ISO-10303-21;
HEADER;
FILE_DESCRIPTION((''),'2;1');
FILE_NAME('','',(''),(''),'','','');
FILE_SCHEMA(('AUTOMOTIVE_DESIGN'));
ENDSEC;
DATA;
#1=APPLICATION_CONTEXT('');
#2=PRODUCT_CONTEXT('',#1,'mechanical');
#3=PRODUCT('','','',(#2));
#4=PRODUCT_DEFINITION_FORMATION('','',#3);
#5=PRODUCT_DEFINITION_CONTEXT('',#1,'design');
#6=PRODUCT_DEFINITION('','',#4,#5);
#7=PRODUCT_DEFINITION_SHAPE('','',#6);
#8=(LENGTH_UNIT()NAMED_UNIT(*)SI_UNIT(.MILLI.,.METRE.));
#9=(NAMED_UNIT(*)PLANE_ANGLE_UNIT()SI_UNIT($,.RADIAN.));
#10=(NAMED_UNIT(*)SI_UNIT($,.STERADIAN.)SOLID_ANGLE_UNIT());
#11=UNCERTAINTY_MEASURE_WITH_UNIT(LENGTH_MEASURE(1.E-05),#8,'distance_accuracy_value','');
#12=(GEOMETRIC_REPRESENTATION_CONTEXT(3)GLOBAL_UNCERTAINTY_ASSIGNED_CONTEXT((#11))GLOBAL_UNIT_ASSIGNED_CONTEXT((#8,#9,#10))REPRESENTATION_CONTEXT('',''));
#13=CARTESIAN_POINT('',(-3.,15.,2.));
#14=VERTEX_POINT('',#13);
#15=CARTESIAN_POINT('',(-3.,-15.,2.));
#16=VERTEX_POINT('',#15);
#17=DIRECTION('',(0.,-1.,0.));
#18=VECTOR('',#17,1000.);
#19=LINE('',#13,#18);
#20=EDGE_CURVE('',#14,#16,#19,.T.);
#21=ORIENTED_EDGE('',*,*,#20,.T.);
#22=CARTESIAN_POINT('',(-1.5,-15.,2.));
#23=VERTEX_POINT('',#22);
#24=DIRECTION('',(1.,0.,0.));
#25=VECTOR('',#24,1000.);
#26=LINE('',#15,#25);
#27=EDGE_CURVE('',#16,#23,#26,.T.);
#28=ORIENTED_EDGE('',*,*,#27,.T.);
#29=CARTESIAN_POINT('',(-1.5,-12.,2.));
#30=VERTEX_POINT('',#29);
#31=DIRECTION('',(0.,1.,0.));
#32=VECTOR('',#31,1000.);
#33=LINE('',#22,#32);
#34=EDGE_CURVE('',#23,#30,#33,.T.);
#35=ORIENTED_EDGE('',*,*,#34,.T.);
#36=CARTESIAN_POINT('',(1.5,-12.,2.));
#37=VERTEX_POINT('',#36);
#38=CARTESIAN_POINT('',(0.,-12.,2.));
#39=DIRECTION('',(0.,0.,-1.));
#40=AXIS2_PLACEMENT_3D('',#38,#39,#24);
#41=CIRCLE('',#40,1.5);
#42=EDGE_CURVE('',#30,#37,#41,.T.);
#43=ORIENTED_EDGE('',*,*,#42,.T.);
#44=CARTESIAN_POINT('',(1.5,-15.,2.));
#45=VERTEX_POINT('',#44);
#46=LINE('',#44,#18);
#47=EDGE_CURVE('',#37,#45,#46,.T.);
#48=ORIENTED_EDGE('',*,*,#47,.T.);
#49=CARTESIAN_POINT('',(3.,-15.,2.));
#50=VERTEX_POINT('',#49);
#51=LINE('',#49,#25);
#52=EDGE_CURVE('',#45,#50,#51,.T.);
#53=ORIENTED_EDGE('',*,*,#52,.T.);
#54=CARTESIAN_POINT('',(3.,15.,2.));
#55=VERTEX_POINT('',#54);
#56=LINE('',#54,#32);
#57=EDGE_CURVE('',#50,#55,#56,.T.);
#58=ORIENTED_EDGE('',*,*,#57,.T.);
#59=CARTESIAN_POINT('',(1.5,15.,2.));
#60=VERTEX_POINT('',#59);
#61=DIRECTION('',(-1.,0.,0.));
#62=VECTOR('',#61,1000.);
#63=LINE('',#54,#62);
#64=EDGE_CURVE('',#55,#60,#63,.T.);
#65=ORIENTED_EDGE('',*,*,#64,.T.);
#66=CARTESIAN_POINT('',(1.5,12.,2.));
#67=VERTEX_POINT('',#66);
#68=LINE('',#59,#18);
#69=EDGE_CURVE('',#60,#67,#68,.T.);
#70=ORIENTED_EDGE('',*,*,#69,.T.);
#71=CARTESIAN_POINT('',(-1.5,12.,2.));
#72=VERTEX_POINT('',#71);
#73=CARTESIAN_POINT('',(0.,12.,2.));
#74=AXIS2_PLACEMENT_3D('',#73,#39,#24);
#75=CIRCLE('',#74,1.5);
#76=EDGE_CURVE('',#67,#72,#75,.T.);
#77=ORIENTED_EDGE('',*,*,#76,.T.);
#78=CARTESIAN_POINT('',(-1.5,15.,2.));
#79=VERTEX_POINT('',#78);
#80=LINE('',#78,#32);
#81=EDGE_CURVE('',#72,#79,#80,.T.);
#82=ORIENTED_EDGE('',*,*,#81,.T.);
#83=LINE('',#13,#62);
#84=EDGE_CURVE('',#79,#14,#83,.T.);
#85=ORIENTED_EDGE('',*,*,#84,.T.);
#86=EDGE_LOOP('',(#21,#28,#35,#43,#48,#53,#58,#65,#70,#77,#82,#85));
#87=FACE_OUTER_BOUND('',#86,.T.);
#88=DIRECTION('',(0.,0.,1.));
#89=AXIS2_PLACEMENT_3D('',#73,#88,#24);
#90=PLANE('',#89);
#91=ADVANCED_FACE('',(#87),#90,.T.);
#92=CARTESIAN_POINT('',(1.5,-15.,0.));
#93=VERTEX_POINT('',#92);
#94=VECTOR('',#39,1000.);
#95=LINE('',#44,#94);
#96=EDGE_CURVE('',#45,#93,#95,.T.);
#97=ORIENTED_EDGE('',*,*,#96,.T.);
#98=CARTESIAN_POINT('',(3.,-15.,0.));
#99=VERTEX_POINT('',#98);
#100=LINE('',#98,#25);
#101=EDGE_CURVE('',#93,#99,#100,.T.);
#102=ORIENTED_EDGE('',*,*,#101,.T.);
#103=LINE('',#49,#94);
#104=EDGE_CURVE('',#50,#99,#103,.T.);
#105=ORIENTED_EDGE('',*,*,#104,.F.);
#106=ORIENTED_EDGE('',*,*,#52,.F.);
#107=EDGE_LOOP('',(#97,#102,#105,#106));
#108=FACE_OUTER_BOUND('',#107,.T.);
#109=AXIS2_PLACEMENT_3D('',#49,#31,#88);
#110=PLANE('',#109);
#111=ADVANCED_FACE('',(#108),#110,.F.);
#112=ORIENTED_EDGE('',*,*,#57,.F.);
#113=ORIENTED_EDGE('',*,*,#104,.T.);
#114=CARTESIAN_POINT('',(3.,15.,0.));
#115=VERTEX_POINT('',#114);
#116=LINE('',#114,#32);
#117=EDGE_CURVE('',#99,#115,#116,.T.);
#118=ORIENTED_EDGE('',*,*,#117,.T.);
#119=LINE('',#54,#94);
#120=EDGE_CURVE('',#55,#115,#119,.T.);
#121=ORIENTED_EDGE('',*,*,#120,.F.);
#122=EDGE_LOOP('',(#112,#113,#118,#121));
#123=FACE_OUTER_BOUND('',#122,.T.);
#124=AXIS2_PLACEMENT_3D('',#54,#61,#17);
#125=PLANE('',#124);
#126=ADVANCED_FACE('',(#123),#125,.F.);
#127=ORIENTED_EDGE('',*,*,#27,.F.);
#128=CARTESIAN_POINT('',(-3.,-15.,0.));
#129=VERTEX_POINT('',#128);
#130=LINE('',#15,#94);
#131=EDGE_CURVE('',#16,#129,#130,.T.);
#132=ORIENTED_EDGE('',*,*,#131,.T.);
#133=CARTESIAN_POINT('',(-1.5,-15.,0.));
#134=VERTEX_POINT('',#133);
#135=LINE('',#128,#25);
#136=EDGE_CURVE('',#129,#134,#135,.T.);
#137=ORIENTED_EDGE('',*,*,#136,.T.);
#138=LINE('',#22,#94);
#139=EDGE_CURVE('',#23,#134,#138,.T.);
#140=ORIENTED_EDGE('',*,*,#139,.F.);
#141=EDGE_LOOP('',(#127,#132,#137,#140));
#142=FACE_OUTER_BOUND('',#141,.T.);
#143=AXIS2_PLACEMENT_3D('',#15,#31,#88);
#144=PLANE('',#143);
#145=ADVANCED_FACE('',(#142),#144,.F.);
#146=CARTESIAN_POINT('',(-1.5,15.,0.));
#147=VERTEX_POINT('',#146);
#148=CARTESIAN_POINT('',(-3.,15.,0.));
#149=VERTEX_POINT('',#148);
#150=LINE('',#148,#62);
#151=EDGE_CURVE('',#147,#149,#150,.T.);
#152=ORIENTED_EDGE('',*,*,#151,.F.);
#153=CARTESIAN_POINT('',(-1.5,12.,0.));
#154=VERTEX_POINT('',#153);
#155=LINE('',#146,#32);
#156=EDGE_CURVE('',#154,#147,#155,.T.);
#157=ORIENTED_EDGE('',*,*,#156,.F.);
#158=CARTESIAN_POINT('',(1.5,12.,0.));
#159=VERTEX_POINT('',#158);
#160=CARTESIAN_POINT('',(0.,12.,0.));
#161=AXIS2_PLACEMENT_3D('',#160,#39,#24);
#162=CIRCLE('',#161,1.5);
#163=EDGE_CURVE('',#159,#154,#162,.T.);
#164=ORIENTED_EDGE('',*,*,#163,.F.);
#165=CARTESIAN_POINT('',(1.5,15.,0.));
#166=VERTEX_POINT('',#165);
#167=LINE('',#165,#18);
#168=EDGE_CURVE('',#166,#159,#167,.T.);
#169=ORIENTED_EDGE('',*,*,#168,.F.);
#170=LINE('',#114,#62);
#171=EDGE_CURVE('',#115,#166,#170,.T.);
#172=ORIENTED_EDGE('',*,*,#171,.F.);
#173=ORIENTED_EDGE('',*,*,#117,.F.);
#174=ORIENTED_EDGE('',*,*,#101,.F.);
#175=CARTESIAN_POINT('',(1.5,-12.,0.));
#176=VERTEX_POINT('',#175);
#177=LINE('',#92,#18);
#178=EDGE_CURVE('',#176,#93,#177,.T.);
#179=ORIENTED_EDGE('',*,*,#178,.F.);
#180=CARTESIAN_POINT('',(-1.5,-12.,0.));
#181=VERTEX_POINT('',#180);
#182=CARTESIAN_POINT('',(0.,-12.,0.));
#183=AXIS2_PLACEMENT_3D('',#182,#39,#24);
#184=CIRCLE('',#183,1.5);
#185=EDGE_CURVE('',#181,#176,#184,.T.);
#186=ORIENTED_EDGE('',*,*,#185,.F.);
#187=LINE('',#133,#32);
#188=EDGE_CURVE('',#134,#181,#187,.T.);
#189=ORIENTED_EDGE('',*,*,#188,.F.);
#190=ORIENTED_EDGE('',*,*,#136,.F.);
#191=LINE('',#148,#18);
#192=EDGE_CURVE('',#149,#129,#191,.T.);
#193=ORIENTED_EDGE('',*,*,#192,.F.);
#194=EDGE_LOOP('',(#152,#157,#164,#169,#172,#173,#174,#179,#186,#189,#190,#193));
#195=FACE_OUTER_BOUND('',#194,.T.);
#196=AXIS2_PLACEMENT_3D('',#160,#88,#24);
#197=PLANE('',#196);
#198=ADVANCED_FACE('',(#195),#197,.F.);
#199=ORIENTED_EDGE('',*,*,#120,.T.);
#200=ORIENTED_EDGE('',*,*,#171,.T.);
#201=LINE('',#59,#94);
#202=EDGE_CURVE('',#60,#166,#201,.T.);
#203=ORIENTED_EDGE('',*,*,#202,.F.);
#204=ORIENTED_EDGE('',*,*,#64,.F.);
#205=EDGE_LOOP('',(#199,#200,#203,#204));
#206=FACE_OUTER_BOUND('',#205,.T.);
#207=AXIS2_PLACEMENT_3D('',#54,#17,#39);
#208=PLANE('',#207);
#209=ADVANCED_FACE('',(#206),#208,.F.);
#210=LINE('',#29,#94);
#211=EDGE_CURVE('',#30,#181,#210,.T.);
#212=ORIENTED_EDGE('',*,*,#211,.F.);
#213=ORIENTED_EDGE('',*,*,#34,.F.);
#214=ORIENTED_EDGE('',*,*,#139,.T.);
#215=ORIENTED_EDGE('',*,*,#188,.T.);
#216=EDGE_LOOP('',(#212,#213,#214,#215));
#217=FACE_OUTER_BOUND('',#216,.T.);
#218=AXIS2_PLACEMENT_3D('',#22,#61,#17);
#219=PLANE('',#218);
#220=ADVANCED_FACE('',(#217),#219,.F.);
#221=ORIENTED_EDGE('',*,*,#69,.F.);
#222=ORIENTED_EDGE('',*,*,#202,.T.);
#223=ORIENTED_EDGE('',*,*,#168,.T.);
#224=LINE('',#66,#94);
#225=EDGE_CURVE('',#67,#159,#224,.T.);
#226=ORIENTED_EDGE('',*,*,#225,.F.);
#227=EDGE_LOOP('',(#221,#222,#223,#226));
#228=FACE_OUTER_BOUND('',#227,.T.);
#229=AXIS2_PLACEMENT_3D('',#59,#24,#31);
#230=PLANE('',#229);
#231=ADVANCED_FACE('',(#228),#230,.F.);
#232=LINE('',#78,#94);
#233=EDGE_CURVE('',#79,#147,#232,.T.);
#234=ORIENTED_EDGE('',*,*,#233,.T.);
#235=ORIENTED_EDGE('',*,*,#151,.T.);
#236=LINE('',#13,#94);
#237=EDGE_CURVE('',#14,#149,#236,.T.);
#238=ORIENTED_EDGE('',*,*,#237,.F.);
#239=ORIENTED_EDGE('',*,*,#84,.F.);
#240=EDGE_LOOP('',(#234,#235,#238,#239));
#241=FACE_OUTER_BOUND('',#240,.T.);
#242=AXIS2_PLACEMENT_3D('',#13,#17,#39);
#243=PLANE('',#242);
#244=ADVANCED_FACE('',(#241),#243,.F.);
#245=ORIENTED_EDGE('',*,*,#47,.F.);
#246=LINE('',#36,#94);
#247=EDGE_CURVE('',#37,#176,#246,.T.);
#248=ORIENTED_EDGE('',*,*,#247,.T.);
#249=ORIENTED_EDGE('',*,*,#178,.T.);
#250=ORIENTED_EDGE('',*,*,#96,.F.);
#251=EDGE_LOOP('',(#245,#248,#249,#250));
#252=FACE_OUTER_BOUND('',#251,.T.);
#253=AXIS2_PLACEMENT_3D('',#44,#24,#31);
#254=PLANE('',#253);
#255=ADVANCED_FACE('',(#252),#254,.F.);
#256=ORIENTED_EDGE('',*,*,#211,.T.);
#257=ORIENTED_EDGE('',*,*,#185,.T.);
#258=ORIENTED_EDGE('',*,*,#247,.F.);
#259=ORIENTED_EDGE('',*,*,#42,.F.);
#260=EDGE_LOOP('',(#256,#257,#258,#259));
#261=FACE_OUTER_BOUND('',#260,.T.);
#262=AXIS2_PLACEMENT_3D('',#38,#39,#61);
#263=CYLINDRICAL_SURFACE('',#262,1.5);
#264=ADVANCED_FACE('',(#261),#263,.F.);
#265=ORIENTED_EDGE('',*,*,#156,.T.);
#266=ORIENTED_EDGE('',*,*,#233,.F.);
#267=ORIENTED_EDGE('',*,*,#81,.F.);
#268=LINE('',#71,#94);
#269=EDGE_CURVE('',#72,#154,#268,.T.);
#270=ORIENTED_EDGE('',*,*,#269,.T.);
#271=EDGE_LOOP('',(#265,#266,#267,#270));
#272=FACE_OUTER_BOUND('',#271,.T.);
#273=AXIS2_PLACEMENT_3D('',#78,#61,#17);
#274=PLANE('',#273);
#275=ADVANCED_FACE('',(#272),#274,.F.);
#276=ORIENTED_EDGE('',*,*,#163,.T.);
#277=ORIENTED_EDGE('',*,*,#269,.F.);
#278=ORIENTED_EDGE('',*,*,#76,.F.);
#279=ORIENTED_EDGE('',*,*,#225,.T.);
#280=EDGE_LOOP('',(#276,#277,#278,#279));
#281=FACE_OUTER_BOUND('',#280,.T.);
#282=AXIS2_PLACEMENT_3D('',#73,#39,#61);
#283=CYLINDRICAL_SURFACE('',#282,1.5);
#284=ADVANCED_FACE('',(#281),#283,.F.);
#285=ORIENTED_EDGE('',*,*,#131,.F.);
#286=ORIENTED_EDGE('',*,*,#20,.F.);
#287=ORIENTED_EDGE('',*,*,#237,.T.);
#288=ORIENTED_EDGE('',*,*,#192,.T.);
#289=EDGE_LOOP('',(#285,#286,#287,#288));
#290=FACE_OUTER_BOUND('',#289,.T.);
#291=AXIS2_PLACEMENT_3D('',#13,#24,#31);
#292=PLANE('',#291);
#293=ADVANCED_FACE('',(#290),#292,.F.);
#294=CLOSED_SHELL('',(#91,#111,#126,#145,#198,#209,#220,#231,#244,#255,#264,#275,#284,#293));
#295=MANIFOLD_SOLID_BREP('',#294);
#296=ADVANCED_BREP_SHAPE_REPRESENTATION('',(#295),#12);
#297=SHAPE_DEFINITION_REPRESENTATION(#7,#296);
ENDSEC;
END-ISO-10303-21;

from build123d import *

# Parameters (mm, degrees)
BOSS_EXTRUDE1_DEPTH = 2


with BuildPart() as part:
    # Sketch1 → Boss-Extrude1 (new body)
    with BuildSketch(Plane.XY):
        with BuildLine():
            Line((3, 15), (3, -15))
            Line((3, -15), (1.5, -15))
            Line((1.5, -15), (1.5, -12))
            ThreePointArc((1.5, -12), (0, -10.5), (-1.5, -12))
            Line((-1.5, -12), (-1.5, -15))
            Line((-1.5, -15), (-3, -15))
            Line((-3, -15), (-3, 15))
            Line((-3, 15), (-1.5, 15))
            Line((-1.5, 15), (-1.5, 12))
            ThreePointArc((-1.5, 12), (0, 10.5), (1.5, 12))
            Line((1.5, 12), (1.5, 15))
            Line((1.5, 15), (3, 15))
        make_face()
    extrude(amount=BOSS_EXTRUDE1_DEPTH)


solid = part.part
